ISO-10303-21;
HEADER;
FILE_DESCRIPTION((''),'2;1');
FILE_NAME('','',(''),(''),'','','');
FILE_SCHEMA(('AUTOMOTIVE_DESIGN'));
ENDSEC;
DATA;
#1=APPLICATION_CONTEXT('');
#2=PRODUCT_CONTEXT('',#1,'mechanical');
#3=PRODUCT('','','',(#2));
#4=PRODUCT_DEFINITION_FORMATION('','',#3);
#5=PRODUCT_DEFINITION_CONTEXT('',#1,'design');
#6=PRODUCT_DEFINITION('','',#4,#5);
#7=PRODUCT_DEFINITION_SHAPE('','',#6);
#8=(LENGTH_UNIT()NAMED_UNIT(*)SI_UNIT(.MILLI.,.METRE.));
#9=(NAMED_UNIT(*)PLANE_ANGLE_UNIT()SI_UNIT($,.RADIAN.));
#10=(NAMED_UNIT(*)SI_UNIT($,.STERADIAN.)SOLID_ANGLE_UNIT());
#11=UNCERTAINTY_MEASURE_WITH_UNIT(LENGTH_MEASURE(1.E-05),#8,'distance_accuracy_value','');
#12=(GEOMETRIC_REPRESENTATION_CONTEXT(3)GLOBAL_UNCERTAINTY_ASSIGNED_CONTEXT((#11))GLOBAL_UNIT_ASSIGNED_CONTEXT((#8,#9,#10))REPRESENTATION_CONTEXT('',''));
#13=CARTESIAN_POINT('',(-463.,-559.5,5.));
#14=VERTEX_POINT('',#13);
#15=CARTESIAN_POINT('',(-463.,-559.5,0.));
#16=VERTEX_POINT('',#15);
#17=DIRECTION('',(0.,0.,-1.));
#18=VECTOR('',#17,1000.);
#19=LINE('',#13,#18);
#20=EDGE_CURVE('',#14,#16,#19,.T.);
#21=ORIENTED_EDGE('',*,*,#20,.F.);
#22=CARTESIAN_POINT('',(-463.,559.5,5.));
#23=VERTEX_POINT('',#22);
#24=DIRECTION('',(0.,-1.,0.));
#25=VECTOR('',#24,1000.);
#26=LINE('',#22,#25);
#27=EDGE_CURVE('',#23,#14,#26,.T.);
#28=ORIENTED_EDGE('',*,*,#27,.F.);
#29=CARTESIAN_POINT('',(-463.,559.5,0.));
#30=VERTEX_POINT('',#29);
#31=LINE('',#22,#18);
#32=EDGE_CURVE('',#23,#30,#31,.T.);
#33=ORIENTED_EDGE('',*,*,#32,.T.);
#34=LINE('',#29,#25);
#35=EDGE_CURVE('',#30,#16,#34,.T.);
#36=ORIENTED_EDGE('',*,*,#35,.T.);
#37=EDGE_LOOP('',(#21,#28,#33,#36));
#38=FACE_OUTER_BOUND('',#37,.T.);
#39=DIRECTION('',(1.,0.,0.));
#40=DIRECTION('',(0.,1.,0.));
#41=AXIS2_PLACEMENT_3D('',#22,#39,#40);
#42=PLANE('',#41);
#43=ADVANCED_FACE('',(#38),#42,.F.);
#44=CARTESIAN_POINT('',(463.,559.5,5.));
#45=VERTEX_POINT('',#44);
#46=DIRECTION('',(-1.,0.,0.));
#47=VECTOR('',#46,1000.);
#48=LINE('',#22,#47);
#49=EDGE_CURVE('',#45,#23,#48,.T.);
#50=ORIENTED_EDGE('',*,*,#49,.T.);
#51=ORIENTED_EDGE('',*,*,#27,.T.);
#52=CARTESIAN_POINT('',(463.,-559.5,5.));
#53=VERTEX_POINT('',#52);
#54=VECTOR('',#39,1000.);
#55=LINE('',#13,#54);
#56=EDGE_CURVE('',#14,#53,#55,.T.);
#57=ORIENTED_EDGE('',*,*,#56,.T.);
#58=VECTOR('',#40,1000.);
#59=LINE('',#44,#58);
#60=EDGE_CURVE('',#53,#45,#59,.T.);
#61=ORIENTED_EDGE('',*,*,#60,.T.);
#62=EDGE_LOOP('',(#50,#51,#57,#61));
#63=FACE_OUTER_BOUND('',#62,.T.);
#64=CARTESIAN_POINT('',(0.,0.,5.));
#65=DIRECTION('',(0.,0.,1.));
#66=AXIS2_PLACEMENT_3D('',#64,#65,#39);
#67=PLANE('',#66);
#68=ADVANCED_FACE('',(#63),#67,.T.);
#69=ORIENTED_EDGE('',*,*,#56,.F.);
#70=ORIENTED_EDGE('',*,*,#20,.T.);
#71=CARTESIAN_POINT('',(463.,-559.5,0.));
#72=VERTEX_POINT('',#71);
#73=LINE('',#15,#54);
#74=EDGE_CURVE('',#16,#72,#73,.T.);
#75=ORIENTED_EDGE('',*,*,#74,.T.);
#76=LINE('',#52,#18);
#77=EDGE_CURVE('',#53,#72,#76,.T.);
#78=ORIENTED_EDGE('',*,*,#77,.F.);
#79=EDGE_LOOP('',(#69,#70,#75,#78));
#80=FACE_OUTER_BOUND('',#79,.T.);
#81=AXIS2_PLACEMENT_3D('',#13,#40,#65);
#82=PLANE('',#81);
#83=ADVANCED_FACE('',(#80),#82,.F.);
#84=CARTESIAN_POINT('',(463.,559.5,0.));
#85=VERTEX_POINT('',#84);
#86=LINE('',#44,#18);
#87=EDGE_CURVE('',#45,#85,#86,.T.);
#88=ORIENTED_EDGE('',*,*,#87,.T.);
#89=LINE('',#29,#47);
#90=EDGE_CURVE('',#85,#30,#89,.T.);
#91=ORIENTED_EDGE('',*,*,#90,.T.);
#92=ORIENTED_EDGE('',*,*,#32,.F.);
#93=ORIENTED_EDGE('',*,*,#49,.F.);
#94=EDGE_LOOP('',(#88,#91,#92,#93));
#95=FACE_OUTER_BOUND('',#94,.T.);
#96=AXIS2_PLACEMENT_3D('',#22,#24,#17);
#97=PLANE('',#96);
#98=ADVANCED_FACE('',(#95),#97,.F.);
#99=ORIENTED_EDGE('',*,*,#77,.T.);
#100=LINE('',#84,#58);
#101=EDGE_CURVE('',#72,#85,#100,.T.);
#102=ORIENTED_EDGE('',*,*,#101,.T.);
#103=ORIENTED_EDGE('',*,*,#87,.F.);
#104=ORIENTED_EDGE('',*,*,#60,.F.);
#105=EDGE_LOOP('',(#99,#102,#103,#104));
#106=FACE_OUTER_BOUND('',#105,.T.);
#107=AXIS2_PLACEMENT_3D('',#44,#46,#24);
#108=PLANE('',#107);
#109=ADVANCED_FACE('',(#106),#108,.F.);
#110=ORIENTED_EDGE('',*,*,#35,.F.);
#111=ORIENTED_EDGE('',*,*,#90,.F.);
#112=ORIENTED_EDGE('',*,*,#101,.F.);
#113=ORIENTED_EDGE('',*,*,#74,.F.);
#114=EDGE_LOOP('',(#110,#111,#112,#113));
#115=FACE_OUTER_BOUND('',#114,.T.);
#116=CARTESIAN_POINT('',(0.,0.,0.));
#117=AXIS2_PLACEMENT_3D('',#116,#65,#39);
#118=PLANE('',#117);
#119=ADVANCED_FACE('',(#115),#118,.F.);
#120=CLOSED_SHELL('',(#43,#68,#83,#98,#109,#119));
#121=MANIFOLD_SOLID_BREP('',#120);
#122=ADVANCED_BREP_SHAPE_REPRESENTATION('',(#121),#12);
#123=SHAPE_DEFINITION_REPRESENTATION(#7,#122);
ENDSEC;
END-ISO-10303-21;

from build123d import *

# Parameters (mm, degrees)
SKETCH_1_W      = 926
SKETCH_1_H      = 1119
EXTRUDE_1_DEPTH = 5


with BuildPart() as part:
    # 草图1 → 凸台-拉伸1 (new body)
    with BuildSketch(Plane.XY):
        Rectangle(SKETCH_1_W, SKETCH_1_H)
    extrude(amount=EXTRUDE_1_DEPTH)


solid = part.part
